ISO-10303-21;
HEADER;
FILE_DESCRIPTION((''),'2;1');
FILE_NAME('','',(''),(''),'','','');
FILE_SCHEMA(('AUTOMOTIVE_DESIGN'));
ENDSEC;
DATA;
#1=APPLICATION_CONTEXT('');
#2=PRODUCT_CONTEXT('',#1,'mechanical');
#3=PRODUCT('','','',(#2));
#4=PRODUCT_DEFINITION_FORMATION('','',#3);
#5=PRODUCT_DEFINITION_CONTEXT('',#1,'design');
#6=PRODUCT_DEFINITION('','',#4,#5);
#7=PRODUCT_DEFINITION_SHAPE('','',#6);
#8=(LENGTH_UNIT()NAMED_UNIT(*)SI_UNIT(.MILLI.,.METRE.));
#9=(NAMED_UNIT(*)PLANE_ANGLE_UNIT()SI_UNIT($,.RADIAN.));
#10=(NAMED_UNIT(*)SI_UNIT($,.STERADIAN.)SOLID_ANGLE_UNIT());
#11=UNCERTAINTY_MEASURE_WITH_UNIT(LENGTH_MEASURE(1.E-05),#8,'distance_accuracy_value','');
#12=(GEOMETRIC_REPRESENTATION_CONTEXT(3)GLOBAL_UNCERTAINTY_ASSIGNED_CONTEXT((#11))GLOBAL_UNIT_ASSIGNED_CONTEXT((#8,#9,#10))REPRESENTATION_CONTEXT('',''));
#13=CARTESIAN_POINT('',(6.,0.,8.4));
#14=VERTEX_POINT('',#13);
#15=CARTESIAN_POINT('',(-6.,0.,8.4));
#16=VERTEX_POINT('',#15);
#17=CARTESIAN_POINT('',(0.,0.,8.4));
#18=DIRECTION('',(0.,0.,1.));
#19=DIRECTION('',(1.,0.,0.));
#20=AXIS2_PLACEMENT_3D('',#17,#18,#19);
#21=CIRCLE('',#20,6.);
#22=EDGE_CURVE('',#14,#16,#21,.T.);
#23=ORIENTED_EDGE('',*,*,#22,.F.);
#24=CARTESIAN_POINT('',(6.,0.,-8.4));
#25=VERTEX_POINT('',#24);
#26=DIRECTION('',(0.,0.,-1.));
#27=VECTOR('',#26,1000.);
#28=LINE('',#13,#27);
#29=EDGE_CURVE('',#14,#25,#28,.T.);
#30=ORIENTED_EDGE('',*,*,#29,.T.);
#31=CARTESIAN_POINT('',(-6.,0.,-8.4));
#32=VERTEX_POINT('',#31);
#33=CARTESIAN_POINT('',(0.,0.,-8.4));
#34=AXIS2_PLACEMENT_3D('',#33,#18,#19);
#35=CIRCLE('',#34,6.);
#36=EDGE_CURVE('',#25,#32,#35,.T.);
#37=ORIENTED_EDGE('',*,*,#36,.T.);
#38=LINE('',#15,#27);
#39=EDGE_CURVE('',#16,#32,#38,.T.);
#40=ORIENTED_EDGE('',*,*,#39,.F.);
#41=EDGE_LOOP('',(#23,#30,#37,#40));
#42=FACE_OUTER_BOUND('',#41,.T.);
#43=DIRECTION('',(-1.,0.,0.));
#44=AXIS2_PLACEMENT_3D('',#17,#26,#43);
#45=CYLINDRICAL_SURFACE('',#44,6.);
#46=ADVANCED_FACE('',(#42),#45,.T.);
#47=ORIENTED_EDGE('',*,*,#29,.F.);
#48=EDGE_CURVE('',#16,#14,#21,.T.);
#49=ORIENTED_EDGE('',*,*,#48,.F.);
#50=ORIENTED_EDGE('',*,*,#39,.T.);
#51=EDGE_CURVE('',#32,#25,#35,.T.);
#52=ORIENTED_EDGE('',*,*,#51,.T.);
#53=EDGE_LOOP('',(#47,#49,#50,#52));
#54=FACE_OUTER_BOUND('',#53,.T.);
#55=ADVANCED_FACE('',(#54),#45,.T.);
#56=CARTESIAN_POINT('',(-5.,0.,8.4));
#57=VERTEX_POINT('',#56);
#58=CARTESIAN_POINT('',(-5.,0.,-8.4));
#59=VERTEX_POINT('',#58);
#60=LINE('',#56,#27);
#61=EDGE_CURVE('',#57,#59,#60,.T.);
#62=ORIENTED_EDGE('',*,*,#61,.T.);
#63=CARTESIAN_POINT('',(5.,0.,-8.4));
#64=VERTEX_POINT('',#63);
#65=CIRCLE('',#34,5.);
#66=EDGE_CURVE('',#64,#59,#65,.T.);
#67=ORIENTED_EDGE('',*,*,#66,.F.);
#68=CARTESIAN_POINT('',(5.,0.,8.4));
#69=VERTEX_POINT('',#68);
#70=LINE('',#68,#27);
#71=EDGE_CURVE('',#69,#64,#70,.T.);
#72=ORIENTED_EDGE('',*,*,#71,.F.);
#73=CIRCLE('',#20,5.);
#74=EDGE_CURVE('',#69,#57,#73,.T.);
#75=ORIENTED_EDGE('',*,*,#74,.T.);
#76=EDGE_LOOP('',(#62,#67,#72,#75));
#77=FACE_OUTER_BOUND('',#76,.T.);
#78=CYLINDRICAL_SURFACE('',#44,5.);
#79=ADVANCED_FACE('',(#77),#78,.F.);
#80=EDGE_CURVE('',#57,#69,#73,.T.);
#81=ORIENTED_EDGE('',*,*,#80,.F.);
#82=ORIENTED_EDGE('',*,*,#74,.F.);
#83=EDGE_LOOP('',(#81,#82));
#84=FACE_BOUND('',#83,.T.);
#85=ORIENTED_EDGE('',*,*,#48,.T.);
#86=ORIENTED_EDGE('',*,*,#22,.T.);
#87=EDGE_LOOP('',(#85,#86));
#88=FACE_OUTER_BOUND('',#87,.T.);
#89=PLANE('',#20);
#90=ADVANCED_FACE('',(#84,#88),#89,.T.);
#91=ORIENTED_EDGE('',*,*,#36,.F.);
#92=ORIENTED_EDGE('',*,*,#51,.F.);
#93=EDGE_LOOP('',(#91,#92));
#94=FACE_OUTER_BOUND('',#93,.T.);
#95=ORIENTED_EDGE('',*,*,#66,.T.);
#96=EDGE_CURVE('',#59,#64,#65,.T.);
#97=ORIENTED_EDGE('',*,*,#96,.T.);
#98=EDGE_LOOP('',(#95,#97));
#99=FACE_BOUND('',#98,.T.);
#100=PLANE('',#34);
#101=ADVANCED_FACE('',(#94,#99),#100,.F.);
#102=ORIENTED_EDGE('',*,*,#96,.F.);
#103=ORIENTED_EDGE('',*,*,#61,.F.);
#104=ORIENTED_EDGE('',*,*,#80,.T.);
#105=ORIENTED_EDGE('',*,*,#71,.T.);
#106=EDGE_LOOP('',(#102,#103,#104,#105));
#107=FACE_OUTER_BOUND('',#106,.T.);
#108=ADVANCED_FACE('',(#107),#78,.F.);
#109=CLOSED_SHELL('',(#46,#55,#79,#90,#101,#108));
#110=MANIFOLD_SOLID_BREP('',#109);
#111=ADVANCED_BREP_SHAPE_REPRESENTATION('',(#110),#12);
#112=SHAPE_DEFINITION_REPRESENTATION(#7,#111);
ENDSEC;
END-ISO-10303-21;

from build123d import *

# Parameters (mm, degrees)
SKETCH1_R           = 6
SKETCH1_R_2         = 5
BOSS_EXTRUDE1_DEPTH = 8.4


with BuildPart() as part:
    # Sketch1 → Boss-Extrude1 (new, symmetric)
    with BuildSketch(Plane.XY):
        Circle(SKETCH1_R)
        Circle(SKETCH1_R_2, mode=Mode.SUBTRACT)
    extrude(amount=BOSS_EXTRUDE1_DEPTH, both=True)


solid = part.part
